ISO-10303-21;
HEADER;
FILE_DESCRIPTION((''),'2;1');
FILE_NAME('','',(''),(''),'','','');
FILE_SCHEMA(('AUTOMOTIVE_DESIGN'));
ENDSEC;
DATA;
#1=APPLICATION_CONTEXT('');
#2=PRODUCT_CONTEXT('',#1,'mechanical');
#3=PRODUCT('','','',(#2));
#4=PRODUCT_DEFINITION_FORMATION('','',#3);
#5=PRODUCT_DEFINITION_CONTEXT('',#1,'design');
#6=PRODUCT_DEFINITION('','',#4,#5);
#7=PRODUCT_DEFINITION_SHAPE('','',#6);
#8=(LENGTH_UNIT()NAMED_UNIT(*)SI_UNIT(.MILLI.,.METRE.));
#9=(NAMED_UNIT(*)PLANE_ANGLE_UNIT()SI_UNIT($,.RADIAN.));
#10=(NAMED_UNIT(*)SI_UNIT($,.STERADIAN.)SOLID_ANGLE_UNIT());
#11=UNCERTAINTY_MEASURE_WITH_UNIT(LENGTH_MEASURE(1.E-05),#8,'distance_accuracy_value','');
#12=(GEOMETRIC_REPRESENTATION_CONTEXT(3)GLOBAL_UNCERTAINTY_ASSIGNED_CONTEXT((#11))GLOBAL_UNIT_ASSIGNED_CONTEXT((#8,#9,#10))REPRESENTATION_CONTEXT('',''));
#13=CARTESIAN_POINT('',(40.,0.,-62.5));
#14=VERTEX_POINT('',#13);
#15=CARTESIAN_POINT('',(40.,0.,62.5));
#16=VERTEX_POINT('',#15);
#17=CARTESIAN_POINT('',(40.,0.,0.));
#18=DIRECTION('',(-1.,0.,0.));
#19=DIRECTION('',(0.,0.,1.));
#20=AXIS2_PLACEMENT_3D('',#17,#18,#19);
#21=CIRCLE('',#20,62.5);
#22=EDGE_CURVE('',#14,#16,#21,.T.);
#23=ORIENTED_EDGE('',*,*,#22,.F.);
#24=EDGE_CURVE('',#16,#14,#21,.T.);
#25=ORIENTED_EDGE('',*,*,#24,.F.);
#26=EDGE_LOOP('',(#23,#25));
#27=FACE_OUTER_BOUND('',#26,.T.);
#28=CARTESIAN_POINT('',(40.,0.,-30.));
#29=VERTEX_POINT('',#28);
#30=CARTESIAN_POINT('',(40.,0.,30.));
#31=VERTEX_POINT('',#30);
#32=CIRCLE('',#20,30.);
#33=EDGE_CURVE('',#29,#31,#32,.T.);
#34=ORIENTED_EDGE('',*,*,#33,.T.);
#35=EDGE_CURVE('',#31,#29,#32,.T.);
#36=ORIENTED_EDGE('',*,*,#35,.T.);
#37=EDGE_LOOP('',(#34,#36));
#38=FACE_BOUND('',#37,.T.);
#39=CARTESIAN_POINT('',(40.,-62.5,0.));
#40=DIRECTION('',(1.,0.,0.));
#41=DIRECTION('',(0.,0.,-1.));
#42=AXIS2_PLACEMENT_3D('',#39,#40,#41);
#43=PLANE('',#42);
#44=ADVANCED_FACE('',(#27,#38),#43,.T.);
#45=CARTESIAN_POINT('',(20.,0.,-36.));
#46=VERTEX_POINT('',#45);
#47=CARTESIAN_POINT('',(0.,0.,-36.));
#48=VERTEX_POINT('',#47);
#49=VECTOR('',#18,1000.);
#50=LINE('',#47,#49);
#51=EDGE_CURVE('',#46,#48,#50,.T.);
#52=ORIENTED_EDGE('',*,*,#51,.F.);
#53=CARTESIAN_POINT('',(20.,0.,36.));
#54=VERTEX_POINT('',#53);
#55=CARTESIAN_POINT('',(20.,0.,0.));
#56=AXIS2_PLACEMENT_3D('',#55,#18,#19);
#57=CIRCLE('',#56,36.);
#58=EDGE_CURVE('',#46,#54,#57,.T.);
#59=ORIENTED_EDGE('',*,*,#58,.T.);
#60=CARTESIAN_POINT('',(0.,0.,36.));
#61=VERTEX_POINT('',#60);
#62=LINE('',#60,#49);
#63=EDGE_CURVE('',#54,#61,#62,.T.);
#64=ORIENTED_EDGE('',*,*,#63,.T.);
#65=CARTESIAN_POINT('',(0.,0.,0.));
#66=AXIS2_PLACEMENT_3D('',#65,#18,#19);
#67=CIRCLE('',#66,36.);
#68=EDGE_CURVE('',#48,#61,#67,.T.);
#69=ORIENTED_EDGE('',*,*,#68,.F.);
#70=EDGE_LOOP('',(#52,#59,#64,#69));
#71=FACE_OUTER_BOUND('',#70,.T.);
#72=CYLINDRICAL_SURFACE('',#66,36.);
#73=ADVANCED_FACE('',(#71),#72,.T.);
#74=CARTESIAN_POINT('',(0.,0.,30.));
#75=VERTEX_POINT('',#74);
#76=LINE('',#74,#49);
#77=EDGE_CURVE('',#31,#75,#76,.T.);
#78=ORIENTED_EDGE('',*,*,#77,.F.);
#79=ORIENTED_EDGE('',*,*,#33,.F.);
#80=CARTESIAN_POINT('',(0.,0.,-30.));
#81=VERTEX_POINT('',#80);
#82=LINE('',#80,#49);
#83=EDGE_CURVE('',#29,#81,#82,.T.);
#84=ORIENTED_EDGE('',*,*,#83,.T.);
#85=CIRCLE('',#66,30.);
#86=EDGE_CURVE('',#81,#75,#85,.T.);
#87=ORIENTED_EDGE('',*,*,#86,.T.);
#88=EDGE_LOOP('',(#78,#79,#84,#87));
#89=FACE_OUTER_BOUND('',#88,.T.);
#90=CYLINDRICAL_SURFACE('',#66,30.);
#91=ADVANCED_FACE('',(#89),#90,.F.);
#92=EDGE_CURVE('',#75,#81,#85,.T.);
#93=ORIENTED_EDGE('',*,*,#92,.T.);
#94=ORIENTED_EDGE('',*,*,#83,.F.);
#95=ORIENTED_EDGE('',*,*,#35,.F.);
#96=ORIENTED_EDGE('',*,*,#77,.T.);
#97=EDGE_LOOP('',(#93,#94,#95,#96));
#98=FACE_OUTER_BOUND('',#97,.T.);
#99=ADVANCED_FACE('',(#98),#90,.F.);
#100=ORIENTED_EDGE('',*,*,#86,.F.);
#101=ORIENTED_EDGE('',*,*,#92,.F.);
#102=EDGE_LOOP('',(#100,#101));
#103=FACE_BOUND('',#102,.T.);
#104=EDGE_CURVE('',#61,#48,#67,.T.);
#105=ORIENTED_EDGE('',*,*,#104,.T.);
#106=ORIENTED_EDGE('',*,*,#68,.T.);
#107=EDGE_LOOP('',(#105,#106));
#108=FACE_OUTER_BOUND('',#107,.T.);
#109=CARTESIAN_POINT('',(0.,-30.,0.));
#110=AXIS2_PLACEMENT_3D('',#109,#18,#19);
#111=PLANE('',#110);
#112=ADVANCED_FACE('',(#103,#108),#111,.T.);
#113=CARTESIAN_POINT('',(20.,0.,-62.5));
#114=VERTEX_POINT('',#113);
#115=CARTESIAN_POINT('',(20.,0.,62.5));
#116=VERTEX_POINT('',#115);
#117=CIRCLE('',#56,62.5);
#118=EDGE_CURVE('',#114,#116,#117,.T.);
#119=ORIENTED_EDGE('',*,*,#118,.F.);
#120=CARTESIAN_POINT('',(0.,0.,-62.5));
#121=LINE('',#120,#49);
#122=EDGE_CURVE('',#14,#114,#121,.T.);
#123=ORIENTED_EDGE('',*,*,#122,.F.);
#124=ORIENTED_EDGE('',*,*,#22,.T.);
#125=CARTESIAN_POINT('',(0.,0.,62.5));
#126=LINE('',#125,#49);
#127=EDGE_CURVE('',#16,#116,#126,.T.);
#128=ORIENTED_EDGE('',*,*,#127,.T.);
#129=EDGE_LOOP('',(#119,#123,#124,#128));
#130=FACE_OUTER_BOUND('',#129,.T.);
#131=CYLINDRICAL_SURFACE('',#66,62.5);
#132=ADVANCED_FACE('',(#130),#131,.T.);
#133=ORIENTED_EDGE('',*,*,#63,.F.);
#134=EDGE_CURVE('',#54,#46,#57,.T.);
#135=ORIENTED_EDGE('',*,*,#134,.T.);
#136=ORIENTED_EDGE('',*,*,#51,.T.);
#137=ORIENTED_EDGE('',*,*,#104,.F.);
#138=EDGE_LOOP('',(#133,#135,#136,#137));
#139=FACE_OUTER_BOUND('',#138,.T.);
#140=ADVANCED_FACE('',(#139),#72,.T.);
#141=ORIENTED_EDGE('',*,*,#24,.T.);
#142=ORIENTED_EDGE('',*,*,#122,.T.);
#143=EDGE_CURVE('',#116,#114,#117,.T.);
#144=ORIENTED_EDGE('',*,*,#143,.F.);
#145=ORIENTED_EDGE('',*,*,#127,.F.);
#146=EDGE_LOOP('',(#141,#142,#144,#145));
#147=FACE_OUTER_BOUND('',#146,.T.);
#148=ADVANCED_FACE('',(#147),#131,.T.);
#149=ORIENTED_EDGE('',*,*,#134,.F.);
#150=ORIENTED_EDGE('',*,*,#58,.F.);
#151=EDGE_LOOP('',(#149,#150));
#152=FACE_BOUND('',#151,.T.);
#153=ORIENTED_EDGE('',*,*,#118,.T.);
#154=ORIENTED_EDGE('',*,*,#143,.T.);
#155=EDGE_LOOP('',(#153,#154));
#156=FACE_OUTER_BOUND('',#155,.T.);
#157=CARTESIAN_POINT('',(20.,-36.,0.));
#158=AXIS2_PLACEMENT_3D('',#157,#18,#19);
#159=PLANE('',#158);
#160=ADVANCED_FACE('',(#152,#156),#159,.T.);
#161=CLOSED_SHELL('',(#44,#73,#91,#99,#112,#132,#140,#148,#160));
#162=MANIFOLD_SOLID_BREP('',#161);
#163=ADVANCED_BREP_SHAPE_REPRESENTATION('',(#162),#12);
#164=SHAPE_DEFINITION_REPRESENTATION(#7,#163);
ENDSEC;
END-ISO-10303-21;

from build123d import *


with BuildPart() as part:
    # Sketch1 → Revolve1 (revolve)
    with BuildSketch(Plane.XY, mode=Mode.PRIVATE) as revolve1_sk:
        Polygon((0, -30), (0, -36), (20, -36), (20, -62.5), (40, -62.5), (40, -30), align=None)
    revolve(revolve1_sk.sketch.rotate(Axis((0, 0, 0), (1, 0, 0)), 270), axis=Axis((0, 0, 0), (1, 0, 0)))


solid = part.part
